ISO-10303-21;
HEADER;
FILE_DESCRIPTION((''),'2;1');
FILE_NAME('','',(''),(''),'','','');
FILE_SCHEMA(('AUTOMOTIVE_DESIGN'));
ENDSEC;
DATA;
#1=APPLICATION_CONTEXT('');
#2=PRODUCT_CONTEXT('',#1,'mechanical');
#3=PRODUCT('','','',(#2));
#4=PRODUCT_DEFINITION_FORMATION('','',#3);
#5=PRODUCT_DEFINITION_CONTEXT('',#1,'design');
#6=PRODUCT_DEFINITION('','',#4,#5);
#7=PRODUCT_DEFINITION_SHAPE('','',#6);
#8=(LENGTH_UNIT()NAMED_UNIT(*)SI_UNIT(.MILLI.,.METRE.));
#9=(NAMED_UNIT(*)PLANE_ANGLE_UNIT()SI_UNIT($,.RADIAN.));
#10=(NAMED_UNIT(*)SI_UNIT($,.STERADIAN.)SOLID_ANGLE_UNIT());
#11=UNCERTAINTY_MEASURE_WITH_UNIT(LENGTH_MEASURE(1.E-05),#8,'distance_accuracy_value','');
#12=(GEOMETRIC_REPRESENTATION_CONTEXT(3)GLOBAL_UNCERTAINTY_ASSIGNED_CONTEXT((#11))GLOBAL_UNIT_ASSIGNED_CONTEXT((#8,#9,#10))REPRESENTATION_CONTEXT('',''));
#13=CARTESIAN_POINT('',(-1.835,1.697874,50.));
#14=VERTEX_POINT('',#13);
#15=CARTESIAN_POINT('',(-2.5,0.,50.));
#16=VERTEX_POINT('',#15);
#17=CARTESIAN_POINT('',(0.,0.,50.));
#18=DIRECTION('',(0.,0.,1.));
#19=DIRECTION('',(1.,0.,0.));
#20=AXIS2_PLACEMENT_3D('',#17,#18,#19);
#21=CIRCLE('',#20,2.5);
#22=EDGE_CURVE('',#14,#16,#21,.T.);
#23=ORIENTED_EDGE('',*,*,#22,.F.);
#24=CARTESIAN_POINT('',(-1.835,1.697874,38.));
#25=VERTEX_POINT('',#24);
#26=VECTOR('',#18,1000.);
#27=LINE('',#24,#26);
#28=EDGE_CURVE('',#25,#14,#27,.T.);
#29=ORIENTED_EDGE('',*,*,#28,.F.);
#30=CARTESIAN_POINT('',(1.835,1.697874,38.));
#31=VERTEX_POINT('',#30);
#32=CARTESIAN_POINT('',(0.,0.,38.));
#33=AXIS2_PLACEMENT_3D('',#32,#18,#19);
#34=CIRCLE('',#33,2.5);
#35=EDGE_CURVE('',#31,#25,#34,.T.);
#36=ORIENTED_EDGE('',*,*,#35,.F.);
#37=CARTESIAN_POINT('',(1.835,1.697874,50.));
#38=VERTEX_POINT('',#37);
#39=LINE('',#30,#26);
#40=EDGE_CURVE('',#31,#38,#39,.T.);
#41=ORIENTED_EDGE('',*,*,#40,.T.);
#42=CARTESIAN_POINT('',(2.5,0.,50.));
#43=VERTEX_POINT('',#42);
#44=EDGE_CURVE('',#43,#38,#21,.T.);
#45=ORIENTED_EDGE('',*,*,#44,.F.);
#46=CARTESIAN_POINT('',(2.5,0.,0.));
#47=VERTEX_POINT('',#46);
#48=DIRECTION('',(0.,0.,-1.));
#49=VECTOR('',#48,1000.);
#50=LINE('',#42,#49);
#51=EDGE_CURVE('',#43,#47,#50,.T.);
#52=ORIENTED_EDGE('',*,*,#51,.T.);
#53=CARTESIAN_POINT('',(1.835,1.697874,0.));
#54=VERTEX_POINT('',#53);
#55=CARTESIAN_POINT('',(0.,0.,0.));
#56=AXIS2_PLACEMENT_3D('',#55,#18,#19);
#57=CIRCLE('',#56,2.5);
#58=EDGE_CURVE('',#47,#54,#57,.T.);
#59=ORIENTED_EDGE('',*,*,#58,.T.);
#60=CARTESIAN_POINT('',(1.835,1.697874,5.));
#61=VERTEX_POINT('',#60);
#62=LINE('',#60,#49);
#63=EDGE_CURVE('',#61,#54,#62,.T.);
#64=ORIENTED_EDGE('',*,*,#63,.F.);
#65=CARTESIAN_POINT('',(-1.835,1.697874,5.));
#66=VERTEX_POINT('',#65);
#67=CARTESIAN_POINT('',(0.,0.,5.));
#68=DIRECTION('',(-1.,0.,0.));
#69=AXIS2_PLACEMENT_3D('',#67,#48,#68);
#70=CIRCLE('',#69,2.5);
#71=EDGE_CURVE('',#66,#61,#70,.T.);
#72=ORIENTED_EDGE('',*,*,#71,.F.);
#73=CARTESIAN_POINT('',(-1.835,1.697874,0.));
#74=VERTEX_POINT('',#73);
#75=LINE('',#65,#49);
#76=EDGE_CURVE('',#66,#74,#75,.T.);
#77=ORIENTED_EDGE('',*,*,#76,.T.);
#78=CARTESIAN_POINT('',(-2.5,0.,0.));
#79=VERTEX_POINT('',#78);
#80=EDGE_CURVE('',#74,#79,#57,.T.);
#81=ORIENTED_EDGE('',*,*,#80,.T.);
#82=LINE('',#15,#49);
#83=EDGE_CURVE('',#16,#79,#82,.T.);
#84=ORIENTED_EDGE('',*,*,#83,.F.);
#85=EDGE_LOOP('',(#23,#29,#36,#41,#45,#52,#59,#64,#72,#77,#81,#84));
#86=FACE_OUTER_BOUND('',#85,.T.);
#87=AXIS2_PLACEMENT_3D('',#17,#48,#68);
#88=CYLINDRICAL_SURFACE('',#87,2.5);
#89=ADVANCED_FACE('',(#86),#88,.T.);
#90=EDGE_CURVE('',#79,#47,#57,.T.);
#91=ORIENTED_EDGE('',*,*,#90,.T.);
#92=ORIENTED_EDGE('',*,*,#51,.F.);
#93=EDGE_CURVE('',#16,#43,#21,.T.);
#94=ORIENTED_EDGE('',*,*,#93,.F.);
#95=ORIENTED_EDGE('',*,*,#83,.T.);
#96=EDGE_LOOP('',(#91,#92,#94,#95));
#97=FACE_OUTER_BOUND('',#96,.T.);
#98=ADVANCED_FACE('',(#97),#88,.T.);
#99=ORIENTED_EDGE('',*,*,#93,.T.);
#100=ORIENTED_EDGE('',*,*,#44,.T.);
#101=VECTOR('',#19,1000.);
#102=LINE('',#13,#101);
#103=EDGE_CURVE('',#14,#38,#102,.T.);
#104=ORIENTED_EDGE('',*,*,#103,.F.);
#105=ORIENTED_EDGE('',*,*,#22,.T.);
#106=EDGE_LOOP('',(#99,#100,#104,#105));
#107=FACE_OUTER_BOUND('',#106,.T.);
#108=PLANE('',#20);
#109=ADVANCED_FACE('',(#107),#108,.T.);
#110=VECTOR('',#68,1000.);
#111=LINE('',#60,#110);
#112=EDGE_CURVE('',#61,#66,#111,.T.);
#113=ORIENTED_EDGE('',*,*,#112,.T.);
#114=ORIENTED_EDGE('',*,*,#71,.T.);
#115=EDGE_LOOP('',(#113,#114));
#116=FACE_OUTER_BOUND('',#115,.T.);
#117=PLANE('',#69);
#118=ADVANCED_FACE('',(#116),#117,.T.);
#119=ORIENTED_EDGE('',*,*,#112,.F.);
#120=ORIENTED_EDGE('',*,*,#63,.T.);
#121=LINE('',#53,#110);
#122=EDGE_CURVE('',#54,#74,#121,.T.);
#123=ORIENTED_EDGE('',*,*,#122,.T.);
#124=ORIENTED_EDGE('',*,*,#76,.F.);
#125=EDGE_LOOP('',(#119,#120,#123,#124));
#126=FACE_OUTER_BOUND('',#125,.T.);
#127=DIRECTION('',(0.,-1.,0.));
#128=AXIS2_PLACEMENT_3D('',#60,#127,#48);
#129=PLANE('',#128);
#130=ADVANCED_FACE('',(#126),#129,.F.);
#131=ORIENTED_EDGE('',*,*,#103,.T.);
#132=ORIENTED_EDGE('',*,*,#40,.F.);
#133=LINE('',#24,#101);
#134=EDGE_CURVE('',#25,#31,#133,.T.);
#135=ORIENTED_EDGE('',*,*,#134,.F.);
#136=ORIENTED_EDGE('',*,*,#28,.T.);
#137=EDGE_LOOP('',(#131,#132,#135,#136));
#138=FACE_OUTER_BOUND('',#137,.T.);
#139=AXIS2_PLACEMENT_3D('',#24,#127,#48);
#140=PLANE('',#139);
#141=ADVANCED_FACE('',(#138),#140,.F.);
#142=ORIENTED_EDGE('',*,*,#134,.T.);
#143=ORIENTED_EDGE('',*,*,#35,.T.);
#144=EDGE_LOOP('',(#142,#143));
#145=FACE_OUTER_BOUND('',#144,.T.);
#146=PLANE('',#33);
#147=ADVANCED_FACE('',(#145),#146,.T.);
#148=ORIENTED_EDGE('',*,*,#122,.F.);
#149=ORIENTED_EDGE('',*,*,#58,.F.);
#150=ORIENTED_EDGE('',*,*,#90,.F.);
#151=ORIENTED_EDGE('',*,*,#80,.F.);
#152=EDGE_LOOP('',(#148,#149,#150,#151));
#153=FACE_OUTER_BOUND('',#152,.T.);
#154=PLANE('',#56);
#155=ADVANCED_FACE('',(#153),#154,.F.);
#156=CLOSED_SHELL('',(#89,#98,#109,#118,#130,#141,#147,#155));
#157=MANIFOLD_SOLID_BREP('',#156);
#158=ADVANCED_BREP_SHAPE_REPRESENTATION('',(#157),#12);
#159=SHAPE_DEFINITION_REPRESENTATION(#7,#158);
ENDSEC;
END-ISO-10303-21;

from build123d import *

# Parameters (mm, degrees)
SKETCH1_R           = 2.5
BOSS_EXTRUDE1_DEPTH = 50
CUT_EXTRUDE1_DEPTH  = 5
CUT_EXTRUDE3_START  = -12
CUT_EXTRUDE3_DEPTH  = 12


with BuildPart() as part:
    # Sketch1 → Boss-Extrude1 (new body)
    with BuildSketch(Plane.XY):
        Circle(SKETCH1_R)
    extrude(amount=BOSS_EXTRUDE1_DEPTH)

    # Sketch2 → Cut-Extrude1 (cut)
    with BuildSketch(Plane(origin=(0, 0, 0), x_dir=(-1, 0, 0), z_dir=(0, 0, -1))):
        with BuildLine():
            Line((-1.835, 1.69787367), (1.835, 1.69787367))
            ThreePointArc((1.835, 1.69787367), (0, 2.5), (-1.835, 1.69787367))
        make_face()
    extrude(amount=-CUT_EXTRUDE1_DEPTH, mode=Mode.SUBTRACT)

    # Sketch3 → Cut-Extrude3 (cut)
    with BuildSketch(Plane.XY.offset(50).offset(CUT_EXTRUDE3_START)):
        with BuildLine():
            Line((-1.835, 1.69787367), (1.835, 1.69787367))
            ThreePointArc((1.835, 1.69787367), (0, 2.5), (-1.835, 1.69787367))
        make_face()
    extrude(amount=CUT_EXTRUDE3_DEPTH, mode=Mode.SUBTRACT)


solid = part.part
